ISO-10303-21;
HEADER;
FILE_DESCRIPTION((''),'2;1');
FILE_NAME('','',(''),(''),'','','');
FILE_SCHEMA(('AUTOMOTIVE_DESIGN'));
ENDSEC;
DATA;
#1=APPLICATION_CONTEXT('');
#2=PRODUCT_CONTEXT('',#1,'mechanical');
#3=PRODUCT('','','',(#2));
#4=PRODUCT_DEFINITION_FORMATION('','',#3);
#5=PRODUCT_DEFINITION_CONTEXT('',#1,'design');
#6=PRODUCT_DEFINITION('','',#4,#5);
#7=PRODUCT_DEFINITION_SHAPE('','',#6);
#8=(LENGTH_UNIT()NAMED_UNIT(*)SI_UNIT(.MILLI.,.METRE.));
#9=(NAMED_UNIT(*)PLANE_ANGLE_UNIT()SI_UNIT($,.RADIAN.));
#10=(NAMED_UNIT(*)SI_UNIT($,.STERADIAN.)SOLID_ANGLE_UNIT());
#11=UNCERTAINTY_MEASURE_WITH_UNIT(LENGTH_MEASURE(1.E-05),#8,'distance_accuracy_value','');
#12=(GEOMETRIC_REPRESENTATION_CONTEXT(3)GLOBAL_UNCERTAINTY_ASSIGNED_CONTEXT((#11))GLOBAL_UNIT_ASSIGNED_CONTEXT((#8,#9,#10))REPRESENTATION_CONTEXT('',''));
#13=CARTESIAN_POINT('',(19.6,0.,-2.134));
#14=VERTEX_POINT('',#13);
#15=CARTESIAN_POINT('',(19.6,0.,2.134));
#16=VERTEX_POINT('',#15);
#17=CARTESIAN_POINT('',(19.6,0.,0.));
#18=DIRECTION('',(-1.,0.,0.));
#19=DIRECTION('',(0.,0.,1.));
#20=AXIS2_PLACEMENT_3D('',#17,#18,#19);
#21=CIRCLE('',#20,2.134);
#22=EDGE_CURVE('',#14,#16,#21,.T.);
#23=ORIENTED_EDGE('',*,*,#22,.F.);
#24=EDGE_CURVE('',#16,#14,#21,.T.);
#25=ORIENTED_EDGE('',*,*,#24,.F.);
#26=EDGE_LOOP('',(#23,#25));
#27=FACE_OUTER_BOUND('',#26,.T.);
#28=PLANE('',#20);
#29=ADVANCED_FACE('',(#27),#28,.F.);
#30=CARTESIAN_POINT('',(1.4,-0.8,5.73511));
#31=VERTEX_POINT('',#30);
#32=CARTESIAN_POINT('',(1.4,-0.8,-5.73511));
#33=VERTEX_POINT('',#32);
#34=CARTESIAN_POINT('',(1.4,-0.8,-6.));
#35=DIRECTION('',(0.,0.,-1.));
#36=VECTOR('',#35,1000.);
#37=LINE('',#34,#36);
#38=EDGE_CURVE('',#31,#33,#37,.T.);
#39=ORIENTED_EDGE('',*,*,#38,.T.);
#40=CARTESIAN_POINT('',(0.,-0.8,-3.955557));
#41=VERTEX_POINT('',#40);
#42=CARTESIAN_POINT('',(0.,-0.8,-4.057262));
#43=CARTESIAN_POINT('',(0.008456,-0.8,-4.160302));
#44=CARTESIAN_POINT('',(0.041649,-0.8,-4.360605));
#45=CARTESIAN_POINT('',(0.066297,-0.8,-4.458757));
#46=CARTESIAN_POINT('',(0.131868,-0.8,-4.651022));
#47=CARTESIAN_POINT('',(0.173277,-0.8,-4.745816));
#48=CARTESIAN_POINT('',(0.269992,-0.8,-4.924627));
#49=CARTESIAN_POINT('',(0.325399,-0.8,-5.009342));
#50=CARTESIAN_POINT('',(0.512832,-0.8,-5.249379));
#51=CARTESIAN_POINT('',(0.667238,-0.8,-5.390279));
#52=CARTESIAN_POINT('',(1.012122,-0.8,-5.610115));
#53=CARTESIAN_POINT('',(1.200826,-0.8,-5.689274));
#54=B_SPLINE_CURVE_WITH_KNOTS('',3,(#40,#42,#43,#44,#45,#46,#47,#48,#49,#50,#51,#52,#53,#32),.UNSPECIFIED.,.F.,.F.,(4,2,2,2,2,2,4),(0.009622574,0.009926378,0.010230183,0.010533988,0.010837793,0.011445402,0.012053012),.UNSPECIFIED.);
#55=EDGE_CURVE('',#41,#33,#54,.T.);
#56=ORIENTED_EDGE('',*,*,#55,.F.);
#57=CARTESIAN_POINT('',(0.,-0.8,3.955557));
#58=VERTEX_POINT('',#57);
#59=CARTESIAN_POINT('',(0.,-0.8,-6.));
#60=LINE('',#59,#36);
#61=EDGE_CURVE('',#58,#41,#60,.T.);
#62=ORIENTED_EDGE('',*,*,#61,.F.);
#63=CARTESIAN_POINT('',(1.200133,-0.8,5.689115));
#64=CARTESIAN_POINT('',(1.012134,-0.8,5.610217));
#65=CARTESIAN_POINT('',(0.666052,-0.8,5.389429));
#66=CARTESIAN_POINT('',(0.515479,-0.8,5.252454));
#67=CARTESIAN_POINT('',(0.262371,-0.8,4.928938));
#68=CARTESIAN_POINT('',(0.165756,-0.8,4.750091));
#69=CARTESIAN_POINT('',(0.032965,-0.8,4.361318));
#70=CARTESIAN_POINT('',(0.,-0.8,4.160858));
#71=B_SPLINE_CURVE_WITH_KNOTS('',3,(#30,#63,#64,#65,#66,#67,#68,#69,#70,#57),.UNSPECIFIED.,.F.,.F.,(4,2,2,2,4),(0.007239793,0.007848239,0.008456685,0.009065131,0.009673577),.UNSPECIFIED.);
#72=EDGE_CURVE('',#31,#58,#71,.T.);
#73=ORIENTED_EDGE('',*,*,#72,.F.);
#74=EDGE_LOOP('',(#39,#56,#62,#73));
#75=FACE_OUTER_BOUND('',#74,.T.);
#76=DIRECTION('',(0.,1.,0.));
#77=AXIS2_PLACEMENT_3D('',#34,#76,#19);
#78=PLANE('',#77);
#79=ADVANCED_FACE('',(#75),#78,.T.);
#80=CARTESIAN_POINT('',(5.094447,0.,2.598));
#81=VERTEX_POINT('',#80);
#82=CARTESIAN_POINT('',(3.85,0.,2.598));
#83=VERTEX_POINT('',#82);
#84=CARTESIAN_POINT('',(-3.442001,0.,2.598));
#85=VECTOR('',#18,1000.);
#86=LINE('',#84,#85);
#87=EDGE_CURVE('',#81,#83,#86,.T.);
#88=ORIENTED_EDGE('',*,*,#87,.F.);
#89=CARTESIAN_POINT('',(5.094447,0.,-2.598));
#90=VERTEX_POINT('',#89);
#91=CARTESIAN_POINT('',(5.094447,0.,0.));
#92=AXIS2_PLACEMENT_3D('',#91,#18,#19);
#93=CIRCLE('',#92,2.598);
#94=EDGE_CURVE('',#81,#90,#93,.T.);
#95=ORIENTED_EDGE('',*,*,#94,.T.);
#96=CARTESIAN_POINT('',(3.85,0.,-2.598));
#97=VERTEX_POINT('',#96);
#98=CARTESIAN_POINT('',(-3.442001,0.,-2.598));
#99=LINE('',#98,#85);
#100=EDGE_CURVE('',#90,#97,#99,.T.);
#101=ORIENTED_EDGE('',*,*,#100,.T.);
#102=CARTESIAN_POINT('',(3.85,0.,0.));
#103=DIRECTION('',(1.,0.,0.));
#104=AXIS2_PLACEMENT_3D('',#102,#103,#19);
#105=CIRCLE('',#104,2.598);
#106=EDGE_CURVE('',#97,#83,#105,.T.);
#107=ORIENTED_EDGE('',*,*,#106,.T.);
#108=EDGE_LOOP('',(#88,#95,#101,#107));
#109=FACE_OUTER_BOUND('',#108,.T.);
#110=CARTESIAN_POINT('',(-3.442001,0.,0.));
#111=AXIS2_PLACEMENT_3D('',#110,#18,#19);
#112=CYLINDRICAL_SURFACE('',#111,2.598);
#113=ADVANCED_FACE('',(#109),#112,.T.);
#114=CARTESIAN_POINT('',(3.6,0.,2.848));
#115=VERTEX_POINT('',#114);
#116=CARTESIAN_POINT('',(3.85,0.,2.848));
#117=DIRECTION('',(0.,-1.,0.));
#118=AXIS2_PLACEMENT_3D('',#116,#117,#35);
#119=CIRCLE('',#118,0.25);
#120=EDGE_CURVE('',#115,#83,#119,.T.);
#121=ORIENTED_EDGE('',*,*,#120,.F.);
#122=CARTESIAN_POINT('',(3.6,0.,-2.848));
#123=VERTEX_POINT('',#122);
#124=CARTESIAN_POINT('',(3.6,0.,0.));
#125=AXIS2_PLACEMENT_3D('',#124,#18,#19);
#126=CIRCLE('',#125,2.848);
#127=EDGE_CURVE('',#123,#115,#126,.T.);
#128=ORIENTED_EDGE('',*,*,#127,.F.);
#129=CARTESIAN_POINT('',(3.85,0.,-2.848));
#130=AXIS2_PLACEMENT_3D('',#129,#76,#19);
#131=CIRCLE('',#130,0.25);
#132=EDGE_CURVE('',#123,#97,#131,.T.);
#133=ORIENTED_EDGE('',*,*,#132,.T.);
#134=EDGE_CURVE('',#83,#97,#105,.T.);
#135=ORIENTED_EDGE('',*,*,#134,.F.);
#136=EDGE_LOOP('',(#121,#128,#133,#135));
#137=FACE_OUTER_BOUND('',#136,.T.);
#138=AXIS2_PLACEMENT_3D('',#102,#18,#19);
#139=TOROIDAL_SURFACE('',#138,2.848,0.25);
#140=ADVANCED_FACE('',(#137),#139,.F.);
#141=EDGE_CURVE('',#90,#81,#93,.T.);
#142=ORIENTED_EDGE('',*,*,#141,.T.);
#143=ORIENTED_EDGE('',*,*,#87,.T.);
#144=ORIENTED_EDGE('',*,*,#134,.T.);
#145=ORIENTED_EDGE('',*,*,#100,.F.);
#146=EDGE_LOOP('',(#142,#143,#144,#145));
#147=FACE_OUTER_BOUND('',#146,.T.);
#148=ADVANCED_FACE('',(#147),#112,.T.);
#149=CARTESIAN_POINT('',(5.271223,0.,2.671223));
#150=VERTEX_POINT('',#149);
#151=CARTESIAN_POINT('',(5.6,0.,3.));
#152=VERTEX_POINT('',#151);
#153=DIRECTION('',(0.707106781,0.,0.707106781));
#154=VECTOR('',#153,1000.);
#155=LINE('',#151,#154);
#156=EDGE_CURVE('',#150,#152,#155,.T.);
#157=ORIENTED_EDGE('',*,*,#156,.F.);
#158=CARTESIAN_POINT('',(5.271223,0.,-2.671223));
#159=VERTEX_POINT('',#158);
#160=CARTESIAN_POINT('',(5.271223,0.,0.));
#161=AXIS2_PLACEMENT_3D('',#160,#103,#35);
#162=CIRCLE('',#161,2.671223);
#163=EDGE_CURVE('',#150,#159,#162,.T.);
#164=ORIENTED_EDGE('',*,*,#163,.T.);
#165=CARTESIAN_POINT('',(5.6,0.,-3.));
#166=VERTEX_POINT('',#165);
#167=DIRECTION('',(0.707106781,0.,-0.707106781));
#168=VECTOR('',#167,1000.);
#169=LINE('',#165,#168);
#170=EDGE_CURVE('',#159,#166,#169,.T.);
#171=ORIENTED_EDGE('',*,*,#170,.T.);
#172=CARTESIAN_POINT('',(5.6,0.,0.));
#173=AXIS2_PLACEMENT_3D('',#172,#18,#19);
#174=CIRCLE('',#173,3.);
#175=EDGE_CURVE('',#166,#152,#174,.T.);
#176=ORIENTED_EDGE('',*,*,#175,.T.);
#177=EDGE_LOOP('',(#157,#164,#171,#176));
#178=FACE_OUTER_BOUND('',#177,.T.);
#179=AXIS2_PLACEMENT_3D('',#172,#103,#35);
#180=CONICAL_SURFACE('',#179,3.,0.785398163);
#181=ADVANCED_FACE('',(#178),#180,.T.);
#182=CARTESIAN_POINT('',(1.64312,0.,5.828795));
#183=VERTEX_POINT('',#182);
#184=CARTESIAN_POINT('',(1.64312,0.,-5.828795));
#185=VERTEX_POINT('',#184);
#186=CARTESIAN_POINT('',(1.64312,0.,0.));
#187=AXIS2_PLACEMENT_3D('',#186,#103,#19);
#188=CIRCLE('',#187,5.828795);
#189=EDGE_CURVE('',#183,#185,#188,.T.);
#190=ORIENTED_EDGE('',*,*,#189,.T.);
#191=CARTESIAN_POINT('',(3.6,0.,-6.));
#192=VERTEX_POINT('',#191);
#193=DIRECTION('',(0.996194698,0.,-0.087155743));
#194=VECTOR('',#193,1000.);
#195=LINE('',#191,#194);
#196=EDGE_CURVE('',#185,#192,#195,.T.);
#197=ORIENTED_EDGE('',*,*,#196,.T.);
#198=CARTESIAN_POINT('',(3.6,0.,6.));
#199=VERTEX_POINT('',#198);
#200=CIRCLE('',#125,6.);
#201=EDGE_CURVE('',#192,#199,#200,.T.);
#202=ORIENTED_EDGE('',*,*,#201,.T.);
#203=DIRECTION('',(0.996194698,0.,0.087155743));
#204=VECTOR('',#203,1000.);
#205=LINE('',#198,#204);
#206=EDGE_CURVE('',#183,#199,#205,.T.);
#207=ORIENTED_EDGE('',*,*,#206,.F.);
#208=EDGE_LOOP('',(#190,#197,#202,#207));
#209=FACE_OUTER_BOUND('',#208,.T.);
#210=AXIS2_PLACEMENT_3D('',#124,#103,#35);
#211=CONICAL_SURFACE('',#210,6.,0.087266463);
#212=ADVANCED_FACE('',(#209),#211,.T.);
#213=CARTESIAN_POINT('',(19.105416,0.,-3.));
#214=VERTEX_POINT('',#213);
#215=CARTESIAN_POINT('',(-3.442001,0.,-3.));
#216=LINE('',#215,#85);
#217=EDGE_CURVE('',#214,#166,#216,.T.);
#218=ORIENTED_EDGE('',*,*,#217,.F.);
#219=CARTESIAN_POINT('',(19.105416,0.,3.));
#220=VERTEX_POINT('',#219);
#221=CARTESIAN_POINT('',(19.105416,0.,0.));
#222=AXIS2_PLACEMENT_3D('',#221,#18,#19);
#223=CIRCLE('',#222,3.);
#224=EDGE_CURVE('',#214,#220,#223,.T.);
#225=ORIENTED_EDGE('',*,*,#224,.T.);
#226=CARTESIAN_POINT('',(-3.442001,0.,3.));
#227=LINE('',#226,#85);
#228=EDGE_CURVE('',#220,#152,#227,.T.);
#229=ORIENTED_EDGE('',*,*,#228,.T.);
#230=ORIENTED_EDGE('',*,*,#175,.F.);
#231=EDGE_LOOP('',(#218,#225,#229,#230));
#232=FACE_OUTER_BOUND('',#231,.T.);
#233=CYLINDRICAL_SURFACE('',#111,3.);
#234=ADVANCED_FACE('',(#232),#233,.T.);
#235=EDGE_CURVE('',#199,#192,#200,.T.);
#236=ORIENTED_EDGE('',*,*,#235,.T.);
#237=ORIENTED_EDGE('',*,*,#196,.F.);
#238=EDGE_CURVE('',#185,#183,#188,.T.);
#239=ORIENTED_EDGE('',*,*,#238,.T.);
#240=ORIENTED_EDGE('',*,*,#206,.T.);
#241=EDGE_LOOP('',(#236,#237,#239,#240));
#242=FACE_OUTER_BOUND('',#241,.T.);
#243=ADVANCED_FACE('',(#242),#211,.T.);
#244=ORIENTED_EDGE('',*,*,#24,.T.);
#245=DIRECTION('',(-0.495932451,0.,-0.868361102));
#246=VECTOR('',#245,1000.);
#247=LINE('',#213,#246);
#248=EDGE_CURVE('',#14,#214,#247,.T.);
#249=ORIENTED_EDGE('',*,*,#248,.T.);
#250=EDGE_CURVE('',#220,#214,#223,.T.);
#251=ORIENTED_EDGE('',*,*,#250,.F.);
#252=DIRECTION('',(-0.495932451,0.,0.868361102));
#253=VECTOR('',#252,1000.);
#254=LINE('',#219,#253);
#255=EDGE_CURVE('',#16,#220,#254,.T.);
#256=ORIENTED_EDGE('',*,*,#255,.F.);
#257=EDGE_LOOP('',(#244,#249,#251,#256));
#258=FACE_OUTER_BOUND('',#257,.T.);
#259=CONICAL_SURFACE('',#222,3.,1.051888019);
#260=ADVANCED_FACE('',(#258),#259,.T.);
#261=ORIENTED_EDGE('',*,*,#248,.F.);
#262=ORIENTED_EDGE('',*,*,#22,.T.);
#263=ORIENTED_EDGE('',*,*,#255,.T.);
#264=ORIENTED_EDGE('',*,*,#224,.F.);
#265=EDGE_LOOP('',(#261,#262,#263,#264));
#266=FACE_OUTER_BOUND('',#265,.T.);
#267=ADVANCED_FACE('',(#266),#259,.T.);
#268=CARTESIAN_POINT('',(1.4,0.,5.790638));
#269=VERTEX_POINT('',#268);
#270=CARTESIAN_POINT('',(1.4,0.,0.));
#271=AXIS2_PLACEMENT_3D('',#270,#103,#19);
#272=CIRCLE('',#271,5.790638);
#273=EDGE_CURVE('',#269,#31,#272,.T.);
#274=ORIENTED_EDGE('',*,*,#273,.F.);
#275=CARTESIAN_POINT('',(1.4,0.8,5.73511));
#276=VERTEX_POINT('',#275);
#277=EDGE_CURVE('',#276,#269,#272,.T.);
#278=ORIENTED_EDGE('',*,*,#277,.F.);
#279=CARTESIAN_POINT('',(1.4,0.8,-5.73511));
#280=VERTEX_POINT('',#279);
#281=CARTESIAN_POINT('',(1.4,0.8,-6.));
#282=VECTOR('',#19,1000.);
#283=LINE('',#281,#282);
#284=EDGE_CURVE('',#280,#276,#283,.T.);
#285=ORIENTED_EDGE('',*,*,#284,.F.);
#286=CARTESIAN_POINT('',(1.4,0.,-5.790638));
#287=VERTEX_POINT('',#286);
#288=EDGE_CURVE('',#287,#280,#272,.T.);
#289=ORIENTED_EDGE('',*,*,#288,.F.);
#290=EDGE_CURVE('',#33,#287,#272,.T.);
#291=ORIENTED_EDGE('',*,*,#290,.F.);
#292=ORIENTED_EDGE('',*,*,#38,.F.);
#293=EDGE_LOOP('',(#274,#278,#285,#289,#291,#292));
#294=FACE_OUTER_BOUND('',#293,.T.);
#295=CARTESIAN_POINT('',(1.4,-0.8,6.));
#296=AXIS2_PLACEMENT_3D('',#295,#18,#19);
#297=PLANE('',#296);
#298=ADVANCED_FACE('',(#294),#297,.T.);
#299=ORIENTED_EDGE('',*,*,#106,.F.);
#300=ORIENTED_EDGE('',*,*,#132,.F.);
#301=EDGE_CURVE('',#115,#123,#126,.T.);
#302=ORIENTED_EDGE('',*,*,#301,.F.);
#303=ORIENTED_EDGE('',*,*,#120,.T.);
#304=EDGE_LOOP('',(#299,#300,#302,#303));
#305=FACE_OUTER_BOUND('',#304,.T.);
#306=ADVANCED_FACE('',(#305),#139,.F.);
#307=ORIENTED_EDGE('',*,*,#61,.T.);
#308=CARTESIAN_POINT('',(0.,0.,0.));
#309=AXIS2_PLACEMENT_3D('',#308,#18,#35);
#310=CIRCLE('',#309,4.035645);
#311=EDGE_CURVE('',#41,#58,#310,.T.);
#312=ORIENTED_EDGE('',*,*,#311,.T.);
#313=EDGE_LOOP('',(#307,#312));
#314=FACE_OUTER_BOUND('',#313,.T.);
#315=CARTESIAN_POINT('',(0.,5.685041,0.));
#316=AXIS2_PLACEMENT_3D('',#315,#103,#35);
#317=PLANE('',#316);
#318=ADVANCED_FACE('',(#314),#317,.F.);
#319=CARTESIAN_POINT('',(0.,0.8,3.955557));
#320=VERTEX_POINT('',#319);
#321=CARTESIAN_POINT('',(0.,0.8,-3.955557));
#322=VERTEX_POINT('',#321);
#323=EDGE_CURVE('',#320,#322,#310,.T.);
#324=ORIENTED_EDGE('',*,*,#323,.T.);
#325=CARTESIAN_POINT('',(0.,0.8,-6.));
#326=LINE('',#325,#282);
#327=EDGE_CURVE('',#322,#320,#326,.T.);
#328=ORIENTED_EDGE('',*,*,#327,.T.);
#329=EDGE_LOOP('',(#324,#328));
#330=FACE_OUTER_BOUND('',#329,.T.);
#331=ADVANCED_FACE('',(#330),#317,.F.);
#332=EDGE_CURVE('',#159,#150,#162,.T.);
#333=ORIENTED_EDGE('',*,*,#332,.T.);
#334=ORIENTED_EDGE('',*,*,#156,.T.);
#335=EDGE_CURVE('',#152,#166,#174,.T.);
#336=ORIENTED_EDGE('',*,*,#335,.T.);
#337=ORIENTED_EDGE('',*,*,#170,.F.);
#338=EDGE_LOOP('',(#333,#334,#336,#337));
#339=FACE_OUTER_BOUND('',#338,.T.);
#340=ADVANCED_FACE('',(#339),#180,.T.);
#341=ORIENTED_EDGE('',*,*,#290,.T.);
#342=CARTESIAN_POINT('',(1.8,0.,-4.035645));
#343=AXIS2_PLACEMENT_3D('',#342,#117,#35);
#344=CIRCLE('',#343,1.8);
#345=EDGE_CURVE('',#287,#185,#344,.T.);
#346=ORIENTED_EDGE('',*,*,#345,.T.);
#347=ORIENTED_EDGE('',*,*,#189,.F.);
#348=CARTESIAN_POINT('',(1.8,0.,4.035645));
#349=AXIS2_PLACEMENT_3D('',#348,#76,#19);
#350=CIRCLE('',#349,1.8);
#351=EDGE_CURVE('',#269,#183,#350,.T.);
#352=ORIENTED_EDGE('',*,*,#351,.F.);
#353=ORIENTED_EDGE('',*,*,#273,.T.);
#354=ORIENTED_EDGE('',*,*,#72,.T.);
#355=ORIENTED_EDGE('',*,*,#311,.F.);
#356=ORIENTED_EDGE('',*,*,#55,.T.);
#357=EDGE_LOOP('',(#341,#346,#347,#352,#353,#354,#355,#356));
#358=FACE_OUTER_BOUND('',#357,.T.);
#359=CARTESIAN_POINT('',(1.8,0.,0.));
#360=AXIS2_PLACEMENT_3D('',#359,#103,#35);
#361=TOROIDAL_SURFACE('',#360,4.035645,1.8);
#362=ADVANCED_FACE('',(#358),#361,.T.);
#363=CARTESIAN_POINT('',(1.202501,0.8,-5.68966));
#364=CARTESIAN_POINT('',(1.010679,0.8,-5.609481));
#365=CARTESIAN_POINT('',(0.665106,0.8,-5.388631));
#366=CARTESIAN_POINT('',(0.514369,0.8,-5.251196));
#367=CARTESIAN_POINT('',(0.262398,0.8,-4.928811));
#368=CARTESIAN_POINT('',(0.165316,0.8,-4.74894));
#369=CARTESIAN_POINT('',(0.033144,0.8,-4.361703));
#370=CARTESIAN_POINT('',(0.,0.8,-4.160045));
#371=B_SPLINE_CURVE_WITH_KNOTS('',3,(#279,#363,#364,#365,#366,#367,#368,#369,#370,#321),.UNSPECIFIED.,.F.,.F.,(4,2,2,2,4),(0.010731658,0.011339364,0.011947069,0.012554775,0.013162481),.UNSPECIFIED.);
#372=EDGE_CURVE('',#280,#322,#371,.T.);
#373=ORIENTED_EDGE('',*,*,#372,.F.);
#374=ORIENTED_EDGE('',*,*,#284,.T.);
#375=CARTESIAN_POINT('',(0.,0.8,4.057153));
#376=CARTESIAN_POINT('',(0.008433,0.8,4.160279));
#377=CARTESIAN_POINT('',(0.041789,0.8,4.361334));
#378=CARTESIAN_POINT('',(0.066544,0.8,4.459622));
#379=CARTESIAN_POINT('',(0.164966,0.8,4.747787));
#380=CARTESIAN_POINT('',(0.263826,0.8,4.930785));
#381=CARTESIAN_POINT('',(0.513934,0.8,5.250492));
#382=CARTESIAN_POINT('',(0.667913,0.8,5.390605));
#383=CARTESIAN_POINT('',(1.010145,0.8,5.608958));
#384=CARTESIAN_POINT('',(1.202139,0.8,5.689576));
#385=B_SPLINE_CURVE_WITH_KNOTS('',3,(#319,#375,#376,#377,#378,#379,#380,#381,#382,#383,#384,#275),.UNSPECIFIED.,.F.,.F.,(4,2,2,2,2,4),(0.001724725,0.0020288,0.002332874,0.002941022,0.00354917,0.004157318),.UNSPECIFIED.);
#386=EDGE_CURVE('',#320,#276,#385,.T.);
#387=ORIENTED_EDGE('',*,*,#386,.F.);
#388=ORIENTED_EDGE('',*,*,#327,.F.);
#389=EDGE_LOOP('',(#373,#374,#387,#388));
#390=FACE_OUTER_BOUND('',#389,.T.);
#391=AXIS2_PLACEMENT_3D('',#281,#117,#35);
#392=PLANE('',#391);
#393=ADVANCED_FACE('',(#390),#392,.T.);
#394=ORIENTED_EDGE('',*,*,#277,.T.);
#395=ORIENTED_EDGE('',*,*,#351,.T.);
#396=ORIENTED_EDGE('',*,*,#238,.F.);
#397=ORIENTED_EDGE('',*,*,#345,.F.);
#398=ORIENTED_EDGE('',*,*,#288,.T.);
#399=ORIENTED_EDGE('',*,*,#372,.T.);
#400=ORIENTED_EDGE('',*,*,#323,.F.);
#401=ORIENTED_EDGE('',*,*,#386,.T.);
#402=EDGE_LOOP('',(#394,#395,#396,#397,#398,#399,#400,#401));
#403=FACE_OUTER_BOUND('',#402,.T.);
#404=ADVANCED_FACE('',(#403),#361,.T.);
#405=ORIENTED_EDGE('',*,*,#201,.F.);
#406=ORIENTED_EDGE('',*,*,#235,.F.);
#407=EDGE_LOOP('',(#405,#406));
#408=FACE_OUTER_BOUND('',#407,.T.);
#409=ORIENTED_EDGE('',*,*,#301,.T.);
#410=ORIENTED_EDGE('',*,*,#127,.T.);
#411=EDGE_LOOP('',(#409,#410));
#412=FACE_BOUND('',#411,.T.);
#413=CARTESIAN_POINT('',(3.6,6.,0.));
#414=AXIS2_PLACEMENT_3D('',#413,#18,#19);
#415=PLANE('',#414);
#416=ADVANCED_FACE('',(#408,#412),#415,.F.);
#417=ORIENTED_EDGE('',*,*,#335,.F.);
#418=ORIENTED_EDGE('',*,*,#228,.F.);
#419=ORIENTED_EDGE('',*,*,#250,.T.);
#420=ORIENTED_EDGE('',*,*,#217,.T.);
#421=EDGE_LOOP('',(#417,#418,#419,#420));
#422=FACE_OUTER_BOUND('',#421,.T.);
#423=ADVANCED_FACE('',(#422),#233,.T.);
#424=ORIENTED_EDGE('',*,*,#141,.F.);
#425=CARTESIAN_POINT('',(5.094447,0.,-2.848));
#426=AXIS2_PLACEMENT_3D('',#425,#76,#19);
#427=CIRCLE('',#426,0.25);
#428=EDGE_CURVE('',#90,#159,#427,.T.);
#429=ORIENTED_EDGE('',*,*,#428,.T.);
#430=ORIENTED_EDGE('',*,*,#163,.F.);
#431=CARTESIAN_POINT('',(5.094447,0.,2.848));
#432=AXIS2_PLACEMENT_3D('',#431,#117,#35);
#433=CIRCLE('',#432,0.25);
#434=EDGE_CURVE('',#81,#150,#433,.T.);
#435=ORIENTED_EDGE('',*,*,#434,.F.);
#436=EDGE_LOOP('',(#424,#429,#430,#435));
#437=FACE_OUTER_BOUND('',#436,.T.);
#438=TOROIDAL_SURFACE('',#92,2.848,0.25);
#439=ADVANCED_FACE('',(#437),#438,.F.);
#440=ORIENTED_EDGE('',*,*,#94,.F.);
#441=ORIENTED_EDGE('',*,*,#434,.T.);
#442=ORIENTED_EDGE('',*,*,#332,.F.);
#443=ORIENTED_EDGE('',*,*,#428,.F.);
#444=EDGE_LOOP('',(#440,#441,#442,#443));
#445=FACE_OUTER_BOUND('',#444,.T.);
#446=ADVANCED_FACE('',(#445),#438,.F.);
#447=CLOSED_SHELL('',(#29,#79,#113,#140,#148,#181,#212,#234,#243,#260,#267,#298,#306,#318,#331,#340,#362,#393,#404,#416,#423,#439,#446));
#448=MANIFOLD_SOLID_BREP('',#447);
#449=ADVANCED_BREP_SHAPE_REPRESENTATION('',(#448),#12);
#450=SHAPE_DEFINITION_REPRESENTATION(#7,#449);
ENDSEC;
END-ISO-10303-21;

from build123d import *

# Parameters (mm, degrees)
FILLET1_R          = 0.25
FILLET2_R          = 1.8
SKETCH5_W          = 12
SKETCH5_H          = 1.6
CUT_EXTRUDE1_DEPTH = 1.4


with BuildPart() as part:
    # Sketch2 → Base-Revolve (revolve)
    with BuildSketch(Plane.XY, mode=Mode.PRIVATE) as base_revolve_sk:
        Polygon((0, 0), (19.6, 0), (19.6, 3), (5.6, 3), (5.198, 2.598), (3.6, 2.598), (3.6, 6), (0, 5.685040811), align=None)
    revolve(base_revolve_sk.sketch.rotate(Axis((-3.442001378, 0, 0), (1, 0, 0)), 90), axis=Axis((-3.442001378, 0, 0), (1, 0, 0)))

    # Fillet1
    fillet1_edges = [part.edges().sort_by_distance(p)[0] for p in [
        (3.6, 0, -2.598),
        (5.198, 0, -2.598),
    ]]
    fillet(fillet1_edges, radius=FILLET1_R)

    # Fillet2
    fillet2_edges = [part.edges().sort_by_distance(p)[0] for p in [
        (0, 0, -5.685040811),
    ]]
    fillet(fillet2_edges, radius=FILLET2_R)

    # Sketch5 → Cut-Extrude1 (cut)
    with BuildSketch(Plane(origin=(0, 0, 0), x_dir=(0, 0, -1), z_dir=(1, 0, 0))):
        Rectangle(SKETCH5_W, SKETCH5_H)
    extrude(amount=CUT_EXTRUDE1_DEPTH, mode=Mode.SUBTRACT)

    # Sketch3 → Cut-Revolve1 (revolve, cut)
    with BuildSketch(Plane.XY, mode=Mode.PRIVATE) as cut_revolve1_sk:
        Polygon((19.105416006, 3), (20.105416006, 3), (19.6, 2.134), align=None)
    revolve(cut_revolve1_sk.sketch.rotate(Axis((-0.122578865, 0, 0), (1, 0, 0)), 90), axis=Axis((-0.122578865, 0, 0), (1, 0, 0)), mode=Mode.SUBTRACT)


solid = part.part
